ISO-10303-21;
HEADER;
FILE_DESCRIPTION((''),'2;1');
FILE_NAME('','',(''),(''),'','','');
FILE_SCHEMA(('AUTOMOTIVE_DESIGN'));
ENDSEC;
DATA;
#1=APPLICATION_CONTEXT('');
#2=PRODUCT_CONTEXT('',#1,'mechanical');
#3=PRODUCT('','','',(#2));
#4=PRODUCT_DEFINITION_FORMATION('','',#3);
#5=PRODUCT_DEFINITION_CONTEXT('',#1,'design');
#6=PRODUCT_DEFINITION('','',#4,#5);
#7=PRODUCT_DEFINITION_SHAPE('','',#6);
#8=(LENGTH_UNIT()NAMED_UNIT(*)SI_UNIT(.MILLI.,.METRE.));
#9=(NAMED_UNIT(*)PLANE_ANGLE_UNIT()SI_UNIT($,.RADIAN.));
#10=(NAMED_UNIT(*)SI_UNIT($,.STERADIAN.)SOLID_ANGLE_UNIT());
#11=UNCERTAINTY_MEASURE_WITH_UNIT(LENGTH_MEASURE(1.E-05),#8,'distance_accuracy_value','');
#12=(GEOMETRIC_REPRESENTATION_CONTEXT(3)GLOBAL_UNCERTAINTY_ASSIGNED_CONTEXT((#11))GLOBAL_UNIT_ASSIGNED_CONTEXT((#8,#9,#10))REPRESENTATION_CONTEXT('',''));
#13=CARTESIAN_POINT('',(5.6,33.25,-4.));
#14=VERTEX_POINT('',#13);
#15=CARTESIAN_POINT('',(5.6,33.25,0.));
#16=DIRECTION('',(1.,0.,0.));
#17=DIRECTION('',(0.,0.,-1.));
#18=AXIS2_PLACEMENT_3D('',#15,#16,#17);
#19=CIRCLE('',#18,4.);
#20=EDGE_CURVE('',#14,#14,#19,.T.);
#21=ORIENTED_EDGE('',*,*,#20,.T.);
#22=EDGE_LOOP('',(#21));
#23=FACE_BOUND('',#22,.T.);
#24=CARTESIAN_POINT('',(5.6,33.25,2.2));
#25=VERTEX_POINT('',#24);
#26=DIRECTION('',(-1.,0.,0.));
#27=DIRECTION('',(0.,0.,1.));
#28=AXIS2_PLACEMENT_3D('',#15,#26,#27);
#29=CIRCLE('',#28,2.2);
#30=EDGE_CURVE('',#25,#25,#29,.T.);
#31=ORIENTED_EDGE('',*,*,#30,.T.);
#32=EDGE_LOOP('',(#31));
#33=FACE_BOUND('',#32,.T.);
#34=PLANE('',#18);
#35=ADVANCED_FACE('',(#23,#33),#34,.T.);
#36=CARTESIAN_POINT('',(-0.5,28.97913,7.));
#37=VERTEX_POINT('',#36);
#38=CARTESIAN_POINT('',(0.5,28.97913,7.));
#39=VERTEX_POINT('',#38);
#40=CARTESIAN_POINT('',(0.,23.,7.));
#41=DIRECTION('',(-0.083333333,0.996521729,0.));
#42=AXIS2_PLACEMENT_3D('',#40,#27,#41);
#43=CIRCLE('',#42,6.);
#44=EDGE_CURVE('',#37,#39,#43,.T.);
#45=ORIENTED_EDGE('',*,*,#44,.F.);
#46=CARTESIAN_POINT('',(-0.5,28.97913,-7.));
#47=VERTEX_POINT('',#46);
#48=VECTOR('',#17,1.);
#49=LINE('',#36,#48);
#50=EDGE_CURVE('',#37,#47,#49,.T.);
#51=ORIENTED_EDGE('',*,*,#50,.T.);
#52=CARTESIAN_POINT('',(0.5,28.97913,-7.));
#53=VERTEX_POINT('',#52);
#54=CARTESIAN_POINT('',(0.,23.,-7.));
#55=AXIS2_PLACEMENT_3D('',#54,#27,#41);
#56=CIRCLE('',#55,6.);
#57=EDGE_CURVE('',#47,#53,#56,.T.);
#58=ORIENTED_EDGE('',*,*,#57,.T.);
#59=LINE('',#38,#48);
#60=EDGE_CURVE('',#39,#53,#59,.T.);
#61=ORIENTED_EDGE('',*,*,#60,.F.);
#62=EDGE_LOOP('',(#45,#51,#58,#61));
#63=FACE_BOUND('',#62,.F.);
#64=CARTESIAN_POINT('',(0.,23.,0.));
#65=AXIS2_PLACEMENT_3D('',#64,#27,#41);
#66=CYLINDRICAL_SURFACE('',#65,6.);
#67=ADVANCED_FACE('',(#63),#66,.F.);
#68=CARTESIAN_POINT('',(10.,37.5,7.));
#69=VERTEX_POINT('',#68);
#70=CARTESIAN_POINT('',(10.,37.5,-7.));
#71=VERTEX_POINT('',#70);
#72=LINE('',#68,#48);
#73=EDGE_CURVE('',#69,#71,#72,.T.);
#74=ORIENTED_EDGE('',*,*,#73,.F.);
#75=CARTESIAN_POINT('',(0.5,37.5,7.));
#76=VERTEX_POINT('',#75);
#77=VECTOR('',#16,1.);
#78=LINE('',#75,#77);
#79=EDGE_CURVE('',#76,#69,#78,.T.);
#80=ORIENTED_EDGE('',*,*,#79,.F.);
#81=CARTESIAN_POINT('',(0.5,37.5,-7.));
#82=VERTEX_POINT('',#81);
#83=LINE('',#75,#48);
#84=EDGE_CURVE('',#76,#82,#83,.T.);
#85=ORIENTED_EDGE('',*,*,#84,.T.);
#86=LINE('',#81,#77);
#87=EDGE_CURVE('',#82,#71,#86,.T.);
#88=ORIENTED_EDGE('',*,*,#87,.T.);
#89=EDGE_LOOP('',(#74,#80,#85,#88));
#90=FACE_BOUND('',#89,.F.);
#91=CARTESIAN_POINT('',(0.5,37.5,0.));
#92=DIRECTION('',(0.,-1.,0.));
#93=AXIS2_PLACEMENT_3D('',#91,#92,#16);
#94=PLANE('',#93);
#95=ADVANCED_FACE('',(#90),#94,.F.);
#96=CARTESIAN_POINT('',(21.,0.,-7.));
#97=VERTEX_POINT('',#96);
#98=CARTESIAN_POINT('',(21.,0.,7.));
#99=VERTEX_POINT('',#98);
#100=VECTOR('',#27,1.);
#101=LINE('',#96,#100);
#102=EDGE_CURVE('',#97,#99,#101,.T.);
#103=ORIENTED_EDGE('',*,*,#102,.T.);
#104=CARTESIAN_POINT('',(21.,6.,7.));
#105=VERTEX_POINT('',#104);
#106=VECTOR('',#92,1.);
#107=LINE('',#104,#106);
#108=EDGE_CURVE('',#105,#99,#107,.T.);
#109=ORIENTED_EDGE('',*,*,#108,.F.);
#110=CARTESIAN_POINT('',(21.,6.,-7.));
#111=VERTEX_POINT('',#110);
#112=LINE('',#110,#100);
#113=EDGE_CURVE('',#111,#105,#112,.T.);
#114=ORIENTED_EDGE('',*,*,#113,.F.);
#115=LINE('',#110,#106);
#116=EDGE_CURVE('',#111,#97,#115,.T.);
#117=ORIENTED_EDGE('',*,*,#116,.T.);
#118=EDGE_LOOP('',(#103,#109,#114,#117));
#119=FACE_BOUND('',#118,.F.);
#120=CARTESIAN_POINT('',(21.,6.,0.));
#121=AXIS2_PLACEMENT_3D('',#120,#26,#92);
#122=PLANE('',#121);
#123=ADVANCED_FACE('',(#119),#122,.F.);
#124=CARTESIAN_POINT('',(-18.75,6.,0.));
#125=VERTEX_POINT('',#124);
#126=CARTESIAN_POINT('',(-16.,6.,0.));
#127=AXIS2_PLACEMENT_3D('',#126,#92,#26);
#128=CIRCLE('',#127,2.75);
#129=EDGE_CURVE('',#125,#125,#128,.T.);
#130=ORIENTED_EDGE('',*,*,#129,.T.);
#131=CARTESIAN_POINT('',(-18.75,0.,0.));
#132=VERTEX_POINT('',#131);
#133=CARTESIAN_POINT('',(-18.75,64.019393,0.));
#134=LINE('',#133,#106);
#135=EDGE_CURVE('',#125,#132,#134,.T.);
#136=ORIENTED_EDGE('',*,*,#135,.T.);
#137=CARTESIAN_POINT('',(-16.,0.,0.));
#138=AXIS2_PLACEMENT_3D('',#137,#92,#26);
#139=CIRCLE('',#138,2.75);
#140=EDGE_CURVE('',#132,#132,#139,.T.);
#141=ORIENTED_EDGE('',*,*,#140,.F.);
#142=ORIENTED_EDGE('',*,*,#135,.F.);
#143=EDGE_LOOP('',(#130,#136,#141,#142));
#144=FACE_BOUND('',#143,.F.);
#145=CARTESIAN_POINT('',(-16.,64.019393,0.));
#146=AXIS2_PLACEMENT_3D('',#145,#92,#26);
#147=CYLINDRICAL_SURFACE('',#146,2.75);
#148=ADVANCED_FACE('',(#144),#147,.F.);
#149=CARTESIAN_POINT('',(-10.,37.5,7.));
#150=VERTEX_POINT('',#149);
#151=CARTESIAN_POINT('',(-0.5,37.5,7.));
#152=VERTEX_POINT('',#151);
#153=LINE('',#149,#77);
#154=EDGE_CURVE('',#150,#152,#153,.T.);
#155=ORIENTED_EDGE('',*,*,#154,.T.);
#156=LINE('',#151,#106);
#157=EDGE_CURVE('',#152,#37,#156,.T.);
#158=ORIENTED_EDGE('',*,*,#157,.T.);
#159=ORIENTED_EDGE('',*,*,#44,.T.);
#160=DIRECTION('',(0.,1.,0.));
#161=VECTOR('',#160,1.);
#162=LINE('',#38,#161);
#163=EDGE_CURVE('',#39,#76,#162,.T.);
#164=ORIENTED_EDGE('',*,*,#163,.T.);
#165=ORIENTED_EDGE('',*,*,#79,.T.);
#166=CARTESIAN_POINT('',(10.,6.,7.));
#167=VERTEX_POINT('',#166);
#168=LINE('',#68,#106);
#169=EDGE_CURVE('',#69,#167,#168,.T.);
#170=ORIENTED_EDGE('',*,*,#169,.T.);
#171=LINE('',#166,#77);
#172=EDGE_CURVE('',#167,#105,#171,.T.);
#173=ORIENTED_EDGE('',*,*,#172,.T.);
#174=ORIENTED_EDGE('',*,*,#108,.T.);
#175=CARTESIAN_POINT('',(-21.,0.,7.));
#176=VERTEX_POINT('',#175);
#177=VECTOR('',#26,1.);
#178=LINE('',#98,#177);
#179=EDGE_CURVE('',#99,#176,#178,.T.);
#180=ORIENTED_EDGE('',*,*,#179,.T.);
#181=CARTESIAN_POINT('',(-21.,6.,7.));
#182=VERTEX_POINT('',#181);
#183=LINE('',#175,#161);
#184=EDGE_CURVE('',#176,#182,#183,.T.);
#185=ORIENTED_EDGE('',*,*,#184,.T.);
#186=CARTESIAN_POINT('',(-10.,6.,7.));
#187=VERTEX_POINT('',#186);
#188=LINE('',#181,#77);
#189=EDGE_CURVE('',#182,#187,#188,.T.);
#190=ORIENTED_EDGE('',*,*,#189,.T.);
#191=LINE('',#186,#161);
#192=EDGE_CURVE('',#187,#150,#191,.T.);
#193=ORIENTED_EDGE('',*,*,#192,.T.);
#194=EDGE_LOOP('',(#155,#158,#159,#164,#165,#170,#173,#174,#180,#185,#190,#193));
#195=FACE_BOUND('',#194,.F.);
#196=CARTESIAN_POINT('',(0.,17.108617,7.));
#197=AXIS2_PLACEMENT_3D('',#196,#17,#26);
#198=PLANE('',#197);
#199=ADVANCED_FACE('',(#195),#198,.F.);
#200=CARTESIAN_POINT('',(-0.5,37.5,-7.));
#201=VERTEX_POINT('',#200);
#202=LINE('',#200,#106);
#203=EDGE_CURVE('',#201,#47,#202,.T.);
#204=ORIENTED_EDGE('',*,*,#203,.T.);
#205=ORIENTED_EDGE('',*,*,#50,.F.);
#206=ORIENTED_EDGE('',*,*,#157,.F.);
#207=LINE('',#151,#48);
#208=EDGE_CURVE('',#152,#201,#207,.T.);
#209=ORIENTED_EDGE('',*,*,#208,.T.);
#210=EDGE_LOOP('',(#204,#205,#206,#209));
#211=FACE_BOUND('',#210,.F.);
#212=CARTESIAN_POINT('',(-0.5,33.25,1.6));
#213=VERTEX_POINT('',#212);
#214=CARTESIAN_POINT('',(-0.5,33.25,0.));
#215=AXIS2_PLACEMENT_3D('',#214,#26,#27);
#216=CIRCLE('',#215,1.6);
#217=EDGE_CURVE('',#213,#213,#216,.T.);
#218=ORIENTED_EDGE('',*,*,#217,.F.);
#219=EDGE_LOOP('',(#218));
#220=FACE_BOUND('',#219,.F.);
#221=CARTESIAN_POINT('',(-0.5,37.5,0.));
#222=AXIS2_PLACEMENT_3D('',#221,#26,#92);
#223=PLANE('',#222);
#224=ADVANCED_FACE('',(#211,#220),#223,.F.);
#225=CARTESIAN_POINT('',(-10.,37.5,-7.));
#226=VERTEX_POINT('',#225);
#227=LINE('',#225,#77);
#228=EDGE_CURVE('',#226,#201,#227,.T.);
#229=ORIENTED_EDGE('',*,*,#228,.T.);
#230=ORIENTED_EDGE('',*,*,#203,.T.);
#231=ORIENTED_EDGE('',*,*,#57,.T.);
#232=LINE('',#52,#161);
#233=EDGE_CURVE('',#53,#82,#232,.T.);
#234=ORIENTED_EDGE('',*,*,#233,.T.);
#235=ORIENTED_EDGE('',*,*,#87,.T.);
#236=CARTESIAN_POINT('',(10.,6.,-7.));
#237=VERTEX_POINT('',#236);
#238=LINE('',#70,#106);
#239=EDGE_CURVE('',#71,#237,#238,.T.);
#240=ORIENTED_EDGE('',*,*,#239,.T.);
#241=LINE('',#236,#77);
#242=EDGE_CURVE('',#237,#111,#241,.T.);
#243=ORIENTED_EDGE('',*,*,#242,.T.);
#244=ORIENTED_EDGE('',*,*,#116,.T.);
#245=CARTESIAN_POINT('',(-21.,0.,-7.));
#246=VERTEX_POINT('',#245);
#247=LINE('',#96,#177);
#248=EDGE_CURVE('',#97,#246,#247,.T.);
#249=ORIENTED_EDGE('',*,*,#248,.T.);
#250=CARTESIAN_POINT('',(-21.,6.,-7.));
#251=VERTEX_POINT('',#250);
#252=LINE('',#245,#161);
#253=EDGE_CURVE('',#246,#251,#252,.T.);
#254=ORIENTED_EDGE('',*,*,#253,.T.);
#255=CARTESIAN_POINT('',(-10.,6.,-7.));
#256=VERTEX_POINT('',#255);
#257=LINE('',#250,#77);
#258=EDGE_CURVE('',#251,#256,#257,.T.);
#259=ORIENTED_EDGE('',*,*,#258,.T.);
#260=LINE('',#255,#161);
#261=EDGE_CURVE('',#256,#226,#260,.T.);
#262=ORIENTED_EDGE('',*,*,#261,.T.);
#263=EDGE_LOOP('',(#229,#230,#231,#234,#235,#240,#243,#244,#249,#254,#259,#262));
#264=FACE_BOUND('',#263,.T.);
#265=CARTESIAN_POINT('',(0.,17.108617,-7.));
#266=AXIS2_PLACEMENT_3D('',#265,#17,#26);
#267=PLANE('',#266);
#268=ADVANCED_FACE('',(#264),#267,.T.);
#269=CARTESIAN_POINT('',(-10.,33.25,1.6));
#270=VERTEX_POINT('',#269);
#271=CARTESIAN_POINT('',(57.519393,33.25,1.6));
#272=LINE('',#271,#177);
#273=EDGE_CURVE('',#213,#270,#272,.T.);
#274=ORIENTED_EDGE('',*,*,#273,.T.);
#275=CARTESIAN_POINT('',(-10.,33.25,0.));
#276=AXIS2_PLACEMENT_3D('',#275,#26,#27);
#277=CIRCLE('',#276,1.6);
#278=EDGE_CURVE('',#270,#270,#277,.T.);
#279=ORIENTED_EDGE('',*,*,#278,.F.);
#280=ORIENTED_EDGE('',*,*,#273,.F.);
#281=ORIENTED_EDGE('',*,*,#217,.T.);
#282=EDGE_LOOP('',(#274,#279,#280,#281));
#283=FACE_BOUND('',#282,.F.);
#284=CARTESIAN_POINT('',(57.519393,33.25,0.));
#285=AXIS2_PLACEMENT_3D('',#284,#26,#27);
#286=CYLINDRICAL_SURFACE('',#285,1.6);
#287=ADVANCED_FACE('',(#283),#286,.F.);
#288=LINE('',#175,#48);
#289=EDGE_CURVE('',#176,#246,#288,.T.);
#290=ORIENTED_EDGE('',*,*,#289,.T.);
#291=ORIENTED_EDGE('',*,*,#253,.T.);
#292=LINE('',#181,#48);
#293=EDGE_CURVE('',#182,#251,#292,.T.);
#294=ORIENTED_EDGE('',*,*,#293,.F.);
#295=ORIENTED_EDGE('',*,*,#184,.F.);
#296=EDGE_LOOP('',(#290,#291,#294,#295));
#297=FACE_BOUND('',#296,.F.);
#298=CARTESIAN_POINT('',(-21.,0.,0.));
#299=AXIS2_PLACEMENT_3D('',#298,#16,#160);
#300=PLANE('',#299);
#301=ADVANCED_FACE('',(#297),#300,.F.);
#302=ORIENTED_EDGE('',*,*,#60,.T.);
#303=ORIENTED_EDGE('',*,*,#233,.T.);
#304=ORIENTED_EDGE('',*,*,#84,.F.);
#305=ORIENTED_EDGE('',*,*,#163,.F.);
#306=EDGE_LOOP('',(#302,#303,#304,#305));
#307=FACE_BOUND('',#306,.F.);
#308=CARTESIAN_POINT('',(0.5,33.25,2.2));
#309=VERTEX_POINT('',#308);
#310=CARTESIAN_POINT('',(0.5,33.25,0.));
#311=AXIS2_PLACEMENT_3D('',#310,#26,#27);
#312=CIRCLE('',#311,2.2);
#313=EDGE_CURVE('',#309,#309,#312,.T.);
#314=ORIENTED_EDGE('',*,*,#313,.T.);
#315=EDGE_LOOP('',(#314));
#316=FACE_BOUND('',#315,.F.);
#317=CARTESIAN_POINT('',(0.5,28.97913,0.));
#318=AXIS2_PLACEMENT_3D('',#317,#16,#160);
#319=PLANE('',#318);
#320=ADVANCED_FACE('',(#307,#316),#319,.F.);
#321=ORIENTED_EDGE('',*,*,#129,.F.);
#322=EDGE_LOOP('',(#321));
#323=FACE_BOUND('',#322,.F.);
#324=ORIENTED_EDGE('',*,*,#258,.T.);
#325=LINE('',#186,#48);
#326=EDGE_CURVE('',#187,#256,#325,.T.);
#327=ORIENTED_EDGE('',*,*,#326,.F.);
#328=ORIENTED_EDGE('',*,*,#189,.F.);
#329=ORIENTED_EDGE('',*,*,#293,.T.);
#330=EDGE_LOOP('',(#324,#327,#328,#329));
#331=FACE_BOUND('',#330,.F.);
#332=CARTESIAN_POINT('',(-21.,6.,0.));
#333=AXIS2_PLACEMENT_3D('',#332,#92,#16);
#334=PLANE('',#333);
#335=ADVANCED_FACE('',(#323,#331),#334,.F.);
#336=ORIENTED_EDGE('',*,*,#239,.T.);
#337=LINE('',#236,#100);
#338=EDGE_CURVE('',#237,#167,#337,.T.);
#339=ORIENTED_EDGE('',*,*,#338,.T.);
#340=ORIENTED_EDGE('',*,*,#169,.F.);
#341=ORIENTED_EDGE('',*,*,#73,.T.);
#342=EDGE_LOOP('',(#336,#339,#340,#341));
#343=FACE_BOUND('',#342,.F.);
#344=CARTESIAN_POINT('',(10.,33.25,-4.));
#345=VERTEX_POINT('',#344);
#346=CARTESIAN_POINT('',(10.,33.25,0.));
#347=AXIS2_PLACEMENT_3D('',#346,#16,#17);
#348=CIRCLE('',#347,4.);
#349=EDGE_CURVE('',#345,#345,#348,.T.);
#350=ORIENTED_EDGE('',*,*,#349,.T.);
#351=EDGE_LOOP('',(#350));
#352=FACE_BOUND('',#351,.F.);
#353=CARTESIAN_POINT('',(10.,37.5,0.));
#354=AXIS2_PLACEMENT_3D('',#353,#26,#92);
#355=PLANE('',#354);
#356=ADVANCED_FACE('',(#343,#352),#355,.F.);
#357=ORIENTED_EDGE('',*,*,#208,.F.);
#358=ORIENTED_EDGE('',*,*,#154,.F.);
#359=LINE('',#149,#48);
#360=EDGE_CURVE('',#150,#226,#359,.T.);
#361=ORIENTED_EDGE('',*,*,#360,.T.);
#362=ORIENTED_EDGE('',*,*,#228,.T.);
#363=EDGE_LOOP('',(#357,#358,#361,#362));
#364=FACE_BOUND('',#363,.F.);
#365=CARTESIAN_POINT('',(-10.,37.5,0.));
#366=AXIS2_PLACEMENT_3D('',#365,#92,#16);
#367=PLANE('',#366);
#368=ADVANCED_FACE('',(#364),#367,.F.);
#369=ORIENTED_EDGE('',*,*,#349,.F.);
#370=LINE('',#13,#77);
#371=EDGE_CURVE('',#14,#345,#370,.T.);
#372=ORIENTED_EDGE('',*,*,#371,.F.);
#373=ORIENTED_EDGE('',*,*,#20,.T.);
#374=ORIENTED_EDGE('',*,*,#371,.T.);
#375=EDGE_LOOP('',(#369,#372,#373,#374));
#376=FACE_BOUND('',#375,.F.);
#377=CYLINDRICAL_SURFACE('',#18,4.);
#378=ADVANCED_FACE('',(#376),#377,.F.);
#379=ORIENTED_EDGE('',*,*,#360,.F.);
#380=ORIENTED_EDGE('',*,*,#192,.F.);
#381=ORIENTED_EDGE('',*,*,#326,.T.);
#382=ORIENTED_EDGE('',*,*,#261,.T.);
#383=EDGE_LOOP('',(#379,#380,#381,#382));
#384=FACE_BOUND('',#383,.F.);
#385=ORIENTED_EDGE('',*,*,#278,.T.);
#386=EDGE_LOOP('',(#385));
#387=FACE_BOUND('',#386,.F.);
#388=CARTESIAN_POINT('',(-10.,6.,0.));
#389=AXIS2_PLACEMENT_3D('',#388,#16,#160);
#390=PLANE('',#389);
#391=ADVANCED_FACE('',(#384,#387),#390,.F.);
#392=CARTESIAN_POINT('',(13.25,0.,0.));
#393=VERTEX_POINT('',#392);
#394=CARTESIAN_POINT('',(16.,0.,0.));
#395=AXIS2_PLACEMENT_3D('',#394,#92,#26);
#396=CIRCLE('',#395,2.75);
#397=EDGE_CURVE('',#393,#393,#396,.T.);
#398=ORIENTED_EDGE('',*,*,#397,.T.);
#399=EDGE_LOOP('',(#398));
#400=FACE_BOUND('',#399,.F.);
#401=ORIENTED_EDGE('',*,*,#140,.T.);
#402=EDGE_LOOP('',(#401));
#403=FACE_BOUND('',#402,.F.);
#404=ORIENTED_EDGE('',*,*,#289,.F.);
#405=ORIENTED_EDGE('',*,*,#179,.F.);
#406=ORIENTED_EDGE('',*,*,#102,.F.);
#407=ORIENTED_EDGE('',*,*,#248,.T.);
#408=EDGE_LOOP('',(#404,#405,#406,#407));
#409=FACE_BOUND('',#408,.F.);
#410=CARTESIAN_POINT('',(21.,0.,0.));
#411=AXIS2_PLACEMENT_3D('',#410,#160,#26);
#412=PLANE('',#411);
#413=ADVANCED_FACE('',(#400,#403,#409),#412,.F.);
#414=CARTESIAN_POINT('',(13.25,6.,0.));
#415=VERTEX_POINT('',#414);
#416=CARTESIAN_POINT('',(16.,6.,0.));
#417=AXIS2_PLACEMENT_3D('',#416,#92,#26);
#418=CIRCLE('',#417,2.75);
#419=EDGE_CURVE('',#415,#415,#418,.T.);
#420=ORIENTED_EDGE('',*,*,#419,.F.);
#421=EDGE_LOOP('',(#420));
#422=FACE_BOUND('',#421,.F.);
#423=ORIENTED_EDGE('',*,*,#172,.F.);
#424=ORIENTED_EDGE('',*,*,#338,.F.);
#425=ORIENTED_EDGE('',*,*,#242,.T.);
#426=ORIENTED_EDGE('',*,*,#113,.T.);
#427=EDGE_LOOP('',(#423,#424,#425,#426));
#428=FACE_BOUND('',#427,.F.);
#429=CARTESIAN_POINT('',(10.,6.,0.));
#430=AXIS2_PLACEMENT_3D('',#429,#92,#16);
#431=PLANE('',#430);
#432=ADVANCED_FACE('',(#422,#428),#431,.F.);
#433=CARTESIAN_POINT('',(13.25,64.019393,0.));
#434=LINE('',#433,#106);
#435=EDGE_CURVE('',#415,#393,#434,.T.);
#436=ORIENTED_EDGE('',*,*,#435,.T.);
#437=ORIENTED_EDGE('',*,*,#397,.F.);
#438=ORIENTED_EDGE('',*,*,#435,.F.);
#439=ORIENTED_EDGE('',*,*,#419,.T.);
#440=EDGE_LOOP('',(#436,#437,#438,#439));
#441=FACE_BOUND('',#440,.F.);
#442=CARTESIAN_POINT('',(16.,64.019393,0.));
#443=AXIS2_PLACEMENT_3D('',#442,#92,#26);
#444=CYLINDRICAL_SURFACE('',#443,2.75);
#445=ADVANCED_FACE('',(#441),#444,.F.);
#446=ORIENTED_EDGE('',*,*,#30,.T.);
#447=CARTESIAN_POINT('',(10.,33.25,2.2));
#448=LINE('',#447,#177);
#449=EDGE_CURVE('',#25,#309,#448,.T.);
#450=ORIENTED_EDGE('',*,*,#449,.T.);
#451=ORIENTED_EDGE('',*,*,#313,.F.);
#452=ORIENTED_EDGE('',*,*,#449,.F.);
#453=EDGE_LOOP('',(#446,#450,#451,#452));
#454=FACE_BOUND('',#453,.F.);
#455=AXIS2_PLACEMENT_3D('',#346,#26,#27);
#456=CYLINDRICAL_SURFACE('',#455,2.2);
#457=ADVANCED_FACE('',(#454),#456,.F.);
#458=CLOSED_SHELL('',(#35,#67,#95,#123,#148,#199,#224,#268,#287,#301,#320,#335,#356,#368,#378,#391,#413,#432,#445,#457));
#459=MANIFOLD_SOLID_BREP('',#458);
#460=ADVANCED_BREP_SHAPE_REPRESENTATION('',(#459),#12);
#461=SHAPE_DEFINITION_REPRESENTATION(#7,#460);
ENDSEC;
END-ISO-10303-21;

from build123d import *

# Parameters (mm, degrees)
EXTRUDE_1_DEPTH           = 7
HOLE_WIZARD_1_D           = 4.4
HOLE_WIZARD_1_DEPTH       = 9.5
HOLE_WIZARD_1_CBORE_D     = 8
HOLE_WIZARD_1_CBORE_DEPTH = 4.4
HOLE_WIZARD_1_2_D         = 5.5
HOLE_WIZARD_1_3_D         = 3.2


with BuildPart() as part:
    # 草图1 → 凸台-拉伸1 (new, symmetric)
    with BuildSketch(Plane.XY):
        with BuildLine():
            Line((21, 0), (-21, 0))
            Line((-21, 0), (-21, 6))
            Line((-21, 6), (-10, 6))
            Line((-10, 6), (-10, 37.5))
            Line((-10, 37.5), (-0.5, 37.5))
            Line((-0.5, 37.5), (-0.5, 28.979130372))
            ThreePointArc((-0.5, 28.979130372), (0, 17), (0.5, 28.979130372))
            Line((0.5, 28.979130372), (0.5, 37.5))
            Line((0.5, 37.5), (10, 37.5))
            Line((10, 37.5), (10, 6))
            Line((10, 6), (21, 6))
            Line((21, 6), (21, 0))
        make_face()
    extrude(amount=EXTRUDE_1_DEPTH, both=True)

    # Hole Wizard 1
    with Locations(Plane(origin=(10, 0, 0), x_dir=(0, 0, -1), z_dir=(1, 0, 0))):
        with Locations((0, 33.25)):
            CounterBoreHole(HOLE_WIZARD_1_D / 2, HOLE_WIZARD_1_CBORE_D / 2, HOLE_WIZARD_1_CBORE_DEPTH, depth=HOLE_WIZARD_1_DEPTH)

    # Hole Wizard 1 2 (through all)
    with Locations(Plane(origin=(0, 6, 0), x_dir=(1, 0, 0), z_dir=(0, 1, 0))):
        with Locations((-16, 0), (16, 0)):
            Hole(HOLE_WIZARD_1_2_D / 2)

    # Hole Wizard 1 3 (through all)
    with Locations(Plane(origin=(-0.5, 0, 0), x_dir=(0, 0, -1), z_dir=(1, 0, 0))):
        with Locations((0, 33.25)):
            Hole(HOLE_WIZARD_1_3_D / 2)


solid = part.part
